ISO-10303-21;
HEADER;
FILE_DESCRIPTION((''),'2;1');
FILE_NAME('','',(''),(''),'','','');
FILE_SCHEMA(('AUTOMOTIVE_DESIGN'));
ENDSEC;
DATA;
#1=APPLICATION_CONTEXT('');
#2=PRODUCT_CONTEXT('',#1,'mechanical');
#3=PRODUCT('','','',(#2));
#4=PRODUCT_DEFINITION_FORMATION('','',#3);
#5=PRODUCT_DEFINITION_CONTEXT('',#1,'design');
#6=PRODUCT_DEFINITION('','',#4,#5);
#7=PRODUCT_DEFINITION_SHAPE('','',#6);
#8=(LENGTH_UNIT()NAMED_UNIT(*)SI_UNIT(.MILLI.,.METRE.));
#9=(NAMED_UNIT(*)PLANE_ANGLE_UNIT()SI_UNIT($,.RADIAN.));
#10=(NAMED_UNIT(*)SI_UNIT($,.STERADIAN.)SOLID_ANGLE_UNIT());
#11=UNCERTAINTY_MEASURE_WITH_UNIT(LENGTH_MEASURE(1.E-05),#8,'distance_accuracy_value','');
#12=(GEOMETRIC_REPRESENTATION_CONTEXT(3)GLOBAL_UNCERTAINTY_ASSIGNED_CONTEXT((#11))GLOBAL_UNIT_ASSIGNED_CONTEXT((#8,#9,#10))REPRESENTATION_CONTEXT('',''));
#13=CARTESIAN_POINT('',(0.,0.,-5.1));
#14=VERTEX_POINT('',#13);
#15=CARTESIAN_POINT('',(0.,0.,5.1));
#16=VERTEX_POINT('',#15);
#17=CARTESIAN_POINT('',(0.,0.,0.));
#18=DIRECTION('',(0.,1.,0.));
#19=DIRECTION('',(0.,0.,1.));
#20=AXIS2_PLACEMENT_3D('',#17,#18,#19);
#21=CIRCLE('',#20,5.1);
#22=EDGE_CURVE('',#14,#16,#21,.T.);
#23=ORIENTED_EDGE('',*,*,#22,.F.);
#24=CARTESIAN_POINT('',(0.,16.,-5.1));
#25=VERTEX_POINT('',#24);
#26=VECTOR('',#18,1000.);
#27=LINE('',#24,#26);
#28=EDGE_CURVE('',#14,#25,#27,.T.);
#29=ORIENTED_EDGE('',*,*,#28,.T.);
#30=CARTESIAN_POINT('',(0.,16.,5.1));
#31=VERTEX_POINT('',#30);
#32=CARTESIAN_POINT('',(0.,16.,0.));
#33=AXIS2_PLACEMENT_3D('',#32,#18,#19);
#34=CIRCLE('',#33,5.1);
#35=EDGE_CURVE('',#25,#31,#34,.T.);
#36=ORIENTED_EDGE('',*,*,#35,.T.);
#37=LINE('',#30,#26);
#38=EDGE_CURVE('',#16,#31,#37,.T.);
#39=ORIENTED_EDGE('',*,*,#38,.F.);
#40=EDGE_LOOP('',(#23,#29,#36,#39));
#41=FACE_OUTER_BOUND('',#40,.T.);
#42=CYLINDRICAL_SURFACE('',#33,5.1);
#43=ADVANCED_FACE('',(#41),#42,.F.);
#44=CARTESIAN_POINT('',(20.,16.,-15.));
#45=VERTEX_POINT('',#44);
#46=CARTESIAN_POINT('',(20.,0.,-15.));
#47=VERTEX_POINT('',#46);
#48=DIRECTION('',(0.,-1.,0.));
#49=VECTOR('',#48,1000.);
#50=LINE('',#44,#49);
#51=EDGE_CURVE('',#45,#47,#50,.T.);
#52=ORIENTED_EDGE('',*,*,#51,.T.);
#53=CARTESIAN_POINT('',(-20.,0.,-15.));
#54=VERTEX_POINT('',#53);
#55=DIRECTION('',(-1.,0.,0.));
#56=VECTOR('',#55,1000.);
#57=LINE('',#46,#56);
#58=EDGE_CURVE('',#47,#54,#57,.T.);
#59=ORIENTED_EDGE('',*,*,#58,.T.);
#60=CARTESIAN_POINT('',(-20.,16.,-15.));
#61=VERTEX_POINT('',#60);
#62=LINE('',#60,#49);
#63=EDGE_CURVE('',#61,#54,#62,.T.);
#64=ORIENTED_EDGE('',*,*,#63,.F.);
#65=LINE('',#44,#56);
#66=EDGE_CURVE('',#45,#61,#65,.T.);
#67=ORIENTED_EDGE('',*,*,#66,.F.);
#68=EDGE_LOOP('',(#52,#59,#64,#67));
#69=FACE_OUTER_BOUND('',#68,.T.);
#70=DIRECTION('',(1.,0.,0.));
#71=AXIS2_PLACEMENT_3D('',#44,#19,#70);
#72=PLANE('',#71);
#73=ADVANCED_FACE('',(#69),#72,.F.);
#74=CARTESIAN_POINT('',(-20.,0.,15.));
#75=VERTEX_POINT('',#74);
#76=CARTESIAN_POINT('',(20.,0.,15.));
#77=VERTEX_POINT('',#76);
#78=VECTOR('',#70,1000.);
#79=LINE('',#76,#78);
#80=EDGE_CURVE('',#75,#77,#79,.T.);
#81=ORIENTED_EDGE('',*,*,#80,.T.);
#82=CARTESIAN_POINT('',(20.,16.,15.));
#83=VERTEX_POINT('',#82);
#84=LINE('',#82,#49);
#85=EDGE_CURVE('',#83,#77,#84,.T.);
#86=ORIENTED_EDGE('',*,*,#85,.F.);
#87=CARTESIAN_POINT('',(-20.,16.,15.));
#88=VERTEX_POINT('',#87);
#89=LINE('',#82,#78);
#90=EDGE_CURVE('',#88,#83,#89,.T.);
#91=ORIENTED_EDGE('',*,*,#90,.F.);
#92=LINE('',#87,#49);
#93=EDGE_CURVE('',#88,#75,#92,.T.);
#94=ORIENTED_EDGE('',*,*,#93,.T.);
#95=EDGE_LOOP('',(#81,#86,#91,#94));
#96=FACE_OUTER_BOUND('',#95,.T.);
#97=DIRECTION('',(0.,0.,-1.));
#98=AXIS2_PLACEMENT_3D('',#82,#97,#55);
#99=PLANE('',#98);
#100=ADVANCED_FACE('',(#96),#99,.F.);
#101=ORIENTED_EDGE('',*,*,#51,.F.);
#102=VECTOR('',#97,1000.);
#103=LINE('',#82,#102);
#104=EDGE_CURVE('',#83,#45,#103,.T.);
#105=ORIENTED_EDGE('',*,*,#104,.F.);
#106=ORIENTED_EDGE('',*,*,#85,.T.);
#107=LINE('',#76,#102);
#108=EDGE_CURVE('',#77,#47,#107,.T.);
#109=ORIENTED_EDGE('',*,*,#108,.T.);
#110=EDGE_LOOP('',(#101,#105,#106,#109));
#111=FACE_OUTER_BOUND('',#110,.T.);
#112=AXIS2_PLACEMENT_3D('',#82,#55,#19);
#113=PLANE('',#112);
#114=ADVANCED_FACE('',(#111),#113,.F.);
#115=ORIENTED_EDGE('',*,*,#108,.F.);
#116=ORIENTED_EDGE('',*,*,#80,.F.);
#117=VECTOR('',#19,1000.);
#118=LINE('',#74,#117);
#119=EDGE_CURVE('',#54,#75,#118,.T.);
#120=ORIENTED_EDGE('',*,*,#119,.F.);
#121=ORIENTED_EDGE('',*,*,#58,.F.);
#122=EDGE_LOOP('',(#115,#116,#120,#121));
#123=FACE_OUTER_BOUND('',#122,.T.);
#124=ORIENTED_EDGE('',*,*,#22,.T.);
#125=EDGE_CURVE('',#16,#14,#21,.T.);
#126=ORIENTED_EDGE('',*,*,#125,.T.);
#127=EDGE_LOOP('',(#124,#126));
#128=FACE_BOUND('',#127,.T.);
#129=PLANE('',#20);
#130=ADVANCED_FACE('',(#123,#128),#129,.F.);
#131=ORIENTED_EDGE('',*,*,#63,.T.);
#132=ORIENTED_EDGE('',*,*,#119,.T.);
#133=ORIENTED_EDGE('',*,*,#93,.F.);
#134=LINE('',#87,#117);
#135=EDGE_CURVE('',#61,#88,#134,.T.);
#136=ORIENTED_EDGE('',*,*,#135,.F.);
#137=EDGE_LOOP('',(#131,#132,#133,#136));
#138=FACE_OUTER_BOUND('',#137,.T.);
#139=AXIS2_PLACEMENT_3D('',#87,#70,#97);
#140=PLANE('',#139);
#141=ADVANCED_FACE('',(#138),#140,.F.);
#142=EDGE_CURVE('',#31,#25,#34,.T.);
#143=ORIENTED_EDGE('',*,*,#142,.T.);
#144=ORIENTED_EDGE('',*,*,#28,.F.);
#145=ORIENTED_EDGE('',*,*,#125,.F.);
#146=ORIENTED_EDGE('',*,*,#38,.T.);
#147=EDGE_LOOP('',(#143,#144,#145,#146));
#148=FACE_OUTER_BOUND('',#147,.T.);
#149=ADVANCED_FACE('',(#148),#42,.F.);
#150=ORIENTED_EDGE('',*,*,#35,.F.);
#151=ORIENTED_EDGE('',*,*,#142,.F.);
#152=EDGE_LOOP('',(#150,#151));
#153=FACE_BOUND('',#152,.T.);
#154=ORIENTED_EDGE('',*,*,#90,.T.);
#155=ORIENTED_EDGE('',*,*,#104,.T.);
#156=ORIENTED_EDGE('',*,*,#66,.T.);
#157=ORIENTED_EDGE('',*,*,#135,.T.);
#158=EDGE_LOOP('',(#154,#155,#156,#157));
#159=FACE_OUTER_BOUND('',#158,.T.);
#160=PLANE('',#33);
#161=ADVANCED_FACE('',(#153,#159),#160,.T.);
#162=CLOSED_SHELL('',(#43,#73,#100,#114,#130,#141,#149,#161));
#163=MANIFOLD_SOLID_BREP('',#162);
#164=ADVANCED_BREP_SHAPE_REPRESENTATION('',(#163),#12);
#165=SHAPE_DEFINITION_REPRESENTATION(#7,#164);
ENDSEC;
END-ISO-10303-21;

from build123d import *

# Parameters (mm, degrees)
SKETCH1_W           = 40
SKETCH1_H           = 30
BOSS_EXTRUDE1_DEPTH = 16
M12_TAPPED_HOLE1_D  = 10.2


with BuildPart() as part:
    # Sketch1 → Boss-Extrude1 (new body)
    with BuildSketch(Plane(origin=(0, 0, 0), x_dir=(1, 0, 0), z_dir=(0, 1, 0))):
        Rectangle(SKETCH1_W, SKETCH1_H)
    extrude(amount=BOSS_EXTRUDE1_DEPTH)

    # M12 Tapped Hole1 (through all)
    with Locations(Plane(origin=(0, 16, 0), x_dir=(1, 0, 0), z_dir=(0, 1, 0))):
        with Locations((0, 0)):
            Hole(M12_TAPPED_HOLE1_D / 2)


solid = part.part
